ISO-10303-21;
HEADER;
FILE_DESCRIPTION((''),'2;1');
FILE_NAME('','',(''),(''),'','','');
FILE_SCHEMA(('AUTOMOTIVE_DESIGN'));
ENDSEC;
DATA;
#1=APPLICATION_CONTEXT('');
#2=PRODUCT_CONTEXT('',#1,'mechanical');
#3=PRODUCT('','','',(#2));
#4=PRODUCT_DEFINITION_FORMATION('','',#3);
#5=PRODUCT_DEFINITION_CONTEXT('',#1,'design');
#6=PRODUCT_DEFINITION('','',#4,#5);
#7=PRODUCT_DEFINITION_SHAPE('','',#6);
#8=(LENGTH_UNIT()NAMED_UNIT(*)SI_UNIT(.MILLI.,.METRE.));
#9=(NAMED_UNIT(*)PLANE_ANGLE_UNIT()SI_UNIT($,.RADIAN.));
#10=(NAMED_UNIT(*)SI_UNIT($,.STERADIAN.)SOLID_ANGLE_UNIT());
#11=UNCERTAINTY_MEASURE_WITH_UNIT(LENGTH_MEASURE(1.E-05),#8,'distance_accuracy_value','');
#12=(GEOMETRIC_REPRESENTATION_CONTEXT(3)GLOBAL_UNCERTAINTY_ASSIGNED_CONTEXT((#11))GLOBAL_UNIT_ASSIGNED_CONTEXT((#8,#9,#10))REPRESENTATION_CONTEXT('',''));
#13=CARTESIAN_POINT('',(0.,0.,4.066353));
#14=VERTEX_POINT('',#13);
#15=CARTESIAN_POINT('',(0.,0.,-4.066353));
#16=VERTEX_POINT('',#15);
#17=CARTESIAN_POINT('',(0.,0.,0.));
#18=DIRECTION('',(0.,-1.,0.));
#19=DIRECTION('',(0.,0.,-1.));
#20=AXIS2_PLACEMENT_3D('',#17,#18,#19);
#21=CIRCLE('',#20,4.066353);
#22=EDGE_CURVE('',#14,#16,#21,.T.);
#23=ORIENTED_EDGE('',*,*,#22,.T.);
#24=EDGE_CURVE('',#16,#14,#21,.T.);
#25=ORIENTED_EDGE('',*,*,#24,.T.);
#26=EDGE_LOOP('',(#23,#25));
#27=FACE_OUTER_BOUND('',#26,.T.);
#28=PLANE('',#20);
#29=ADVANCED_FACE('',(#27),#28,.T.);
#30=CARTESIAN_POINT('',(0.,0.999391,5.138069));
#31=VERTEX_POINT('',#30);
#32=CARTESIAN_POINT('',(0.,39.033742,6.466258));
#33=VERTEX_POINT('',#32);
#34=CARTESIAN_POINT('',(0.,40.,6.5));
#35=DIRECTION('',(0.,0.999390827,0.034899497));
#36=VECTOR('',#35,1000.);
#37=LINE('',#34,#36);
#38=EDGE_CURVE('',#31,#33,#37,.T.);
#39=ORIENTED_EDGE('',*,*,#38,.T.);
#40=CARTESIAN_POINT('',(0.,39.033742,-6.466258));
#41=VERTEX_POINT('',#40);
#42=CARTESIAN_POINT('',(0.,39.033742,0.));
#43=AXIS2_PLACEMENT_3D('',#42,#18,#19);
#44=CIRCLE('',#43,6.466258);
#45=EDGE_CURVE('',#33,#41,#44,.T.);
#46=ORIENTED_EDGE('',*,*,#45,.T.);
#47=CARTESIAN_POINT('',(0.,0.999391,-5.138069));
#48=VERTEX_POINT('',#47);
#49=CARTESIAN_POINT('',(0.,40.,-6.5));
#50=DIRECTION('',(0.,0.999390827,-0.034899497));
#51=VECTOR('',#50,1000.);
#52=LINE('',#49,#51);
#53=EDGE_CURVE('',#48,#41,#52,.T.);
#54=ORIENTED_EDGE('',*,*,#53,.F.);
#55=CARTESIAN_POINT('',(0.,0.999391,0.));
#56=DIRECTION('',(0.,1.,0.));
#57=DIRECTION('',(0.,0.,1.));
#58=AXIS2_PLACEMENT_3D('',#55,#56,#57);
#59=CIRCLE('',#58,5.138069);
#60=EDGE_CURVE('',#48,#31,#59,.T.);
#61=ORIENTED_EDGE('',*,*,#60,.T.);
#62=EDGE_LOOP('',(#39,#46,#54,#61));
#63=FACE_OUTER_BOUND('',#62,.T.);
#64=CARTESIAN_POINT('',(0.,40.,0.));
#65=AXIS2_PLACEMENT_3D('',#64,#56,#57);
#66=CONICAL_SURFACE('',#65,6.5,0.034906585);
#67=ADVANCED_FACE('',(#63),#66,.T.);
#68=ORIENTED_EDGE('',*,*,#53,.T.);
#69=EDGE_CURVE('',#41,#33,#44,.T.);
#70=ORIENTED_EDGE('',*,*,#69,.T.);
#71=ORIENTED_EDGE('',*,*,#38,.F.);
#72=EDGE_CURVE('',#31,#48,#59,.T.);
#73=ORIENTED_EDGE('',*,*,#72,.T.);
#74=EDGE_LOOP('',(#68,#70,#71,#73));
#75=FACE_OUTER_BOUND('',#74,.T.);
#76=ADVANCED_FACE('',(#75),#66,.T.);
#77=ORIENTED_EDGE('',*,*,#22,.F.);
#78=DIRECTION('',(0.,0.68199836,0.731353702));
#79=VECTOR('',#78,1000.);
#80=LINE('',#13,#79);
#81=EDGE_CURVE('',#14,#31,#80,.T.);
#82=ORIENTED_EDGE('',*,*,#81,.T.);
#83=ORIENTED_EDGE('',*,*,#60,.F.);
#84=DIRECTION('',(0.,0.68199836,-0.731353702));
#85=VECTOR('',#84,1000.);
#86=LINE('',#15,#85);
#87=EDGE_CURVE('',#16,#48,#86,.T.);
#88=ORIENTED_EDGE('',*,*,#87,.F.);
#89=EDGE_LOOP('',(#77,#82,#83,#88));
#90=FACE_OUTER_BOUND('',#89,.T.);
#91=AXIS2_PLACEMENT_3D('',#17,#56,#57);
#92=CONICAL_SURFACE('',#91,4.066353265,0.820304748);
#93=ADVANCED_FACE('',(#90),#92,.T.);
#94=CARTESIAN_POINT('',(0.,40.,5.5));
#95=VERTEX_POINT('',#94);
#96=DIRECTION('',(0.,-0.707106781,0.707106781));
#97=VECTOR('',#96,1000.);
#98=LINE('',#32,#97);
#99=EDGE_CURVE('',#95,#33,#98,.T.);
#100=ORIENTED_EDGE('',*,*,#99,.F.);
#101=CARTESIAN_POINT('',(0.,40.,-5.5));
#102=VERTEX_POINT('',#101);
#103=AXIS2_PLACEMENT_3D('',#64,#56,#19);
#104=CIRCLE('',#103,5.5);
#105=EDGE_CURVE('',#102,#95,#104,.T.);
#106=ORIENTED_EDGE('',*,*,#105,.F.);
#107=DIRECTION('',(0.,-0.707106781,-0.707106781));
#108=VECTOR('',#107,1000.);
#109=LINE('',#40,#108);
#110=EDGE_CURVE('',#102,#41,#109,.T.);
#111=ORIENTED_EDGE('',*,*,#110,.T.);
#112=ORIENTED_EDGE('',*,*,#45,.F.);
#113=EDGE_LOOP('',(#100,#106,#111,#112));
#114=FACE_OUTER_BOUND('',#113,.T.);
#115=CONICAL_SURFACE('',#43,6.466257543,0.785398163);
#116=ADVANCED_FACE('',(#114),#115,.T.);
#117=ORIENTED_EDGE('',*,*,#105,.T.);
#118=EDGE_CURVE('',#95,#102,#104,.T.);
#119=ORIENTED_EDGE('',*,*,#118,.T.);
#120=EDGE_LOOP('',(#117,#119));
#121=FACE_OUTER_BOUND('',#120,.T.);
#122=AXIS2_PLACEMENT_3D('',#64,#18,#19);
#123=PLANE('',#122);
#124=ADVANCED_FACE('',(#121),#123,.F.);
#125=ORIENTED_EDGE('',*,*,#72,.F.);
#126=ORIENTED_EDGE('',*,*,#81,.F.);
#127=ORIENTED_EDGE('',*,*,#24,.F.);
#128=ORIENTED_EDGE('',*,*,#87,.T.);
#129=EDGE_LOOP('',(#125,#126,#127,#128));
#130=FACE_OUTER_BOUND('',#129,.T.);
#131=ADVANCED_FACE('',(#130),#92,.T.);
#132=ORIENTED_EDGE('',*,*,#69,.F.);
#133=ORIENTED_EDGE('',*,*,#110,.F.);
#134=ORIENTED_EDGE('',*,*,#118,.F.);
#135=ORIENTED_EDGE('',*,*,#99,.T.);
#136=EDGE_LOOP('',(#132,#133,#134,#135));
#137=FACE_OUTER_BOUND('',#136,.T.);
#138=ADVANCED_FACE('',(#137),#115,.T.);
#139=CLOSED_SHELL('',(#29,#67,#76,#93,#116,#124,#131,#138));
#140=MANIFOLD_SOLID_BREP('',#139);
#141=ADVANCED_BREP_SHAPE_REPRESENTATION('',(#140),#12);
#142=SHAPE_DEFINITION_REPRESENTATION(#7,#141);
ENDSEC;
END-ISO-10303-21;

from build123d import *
from OCP.BRepFilletAPI import BRepFilletAPI_MakeChamfer

# Parameters (mm, degrees)
CHAMFER1_SIZE    = 1
CHAMFER1_SIZE2   = 1.036815955
CHAMFER1_SIZE2_2 = 0.96684652


with BuildPart() as part:
    # Sketch1 → Revolve4 (revolve)
    with BuildSketch(Plane.XY, mode=Mode.PRIVATE) as revolve4_sk:
        Polygon((6.5, 40), (5.10316922, 0), (0, 0), (0, 40), align=None)
    revolve(revolve4_sk.sketch.rotate(Axis((0, 0, 0), (0, 1, 0)), 90), axis=Axis((0, 0, 0), (0, 1, 0)))

    # Chamfer1: one chamfer whose edges measure the first distance from different faces: ONE call of the kernel's chamfer builder (chamfer() names one face for all edges)
    chamfer1_edges_1 = [part.edges().sort_by_distance(p)[0] for p in [
        (0, 0, 5.10316922),
    ]]
    chamfer1_side_1 = [part.faces().sort_by_distance(p)[0] for p in [
        (0, 20, 5.80158461),
    ]]
    chamfer1_edges_2 = [part.edges().sort_by_distance(p)[0] for p in [
        (0, 40, 6.5),
    ]]
    chamfer1_side_2 = [part.faces().sort_by_distance(p)[0] for p in [
        (0, 40, 0),
    ]]
    chamfer1 = BRepFilletAPI_MakeChamfer(part.part.solid().wrapped)
    for e in chamfer1_edges_1:
        chamfer1.Add(CHAMFER1_SIZE, CHAMFER1_SIZE2, e.wrapped, chamfer1_side_1[0].wrapped)  # the first distance lies on this face
    for e in chamfer1_edges_2:
        chamfer1.Add(CHAMFER1_SIZE, CHAMFER1_SIZE2_2, e.wrapped, chamfer1_side_2[0].wrapped)  # the first distance lies on this face
    add(Compound.cast(chamfer1.Shape()), mode=Mode.REPLACE)


solid = part.part
